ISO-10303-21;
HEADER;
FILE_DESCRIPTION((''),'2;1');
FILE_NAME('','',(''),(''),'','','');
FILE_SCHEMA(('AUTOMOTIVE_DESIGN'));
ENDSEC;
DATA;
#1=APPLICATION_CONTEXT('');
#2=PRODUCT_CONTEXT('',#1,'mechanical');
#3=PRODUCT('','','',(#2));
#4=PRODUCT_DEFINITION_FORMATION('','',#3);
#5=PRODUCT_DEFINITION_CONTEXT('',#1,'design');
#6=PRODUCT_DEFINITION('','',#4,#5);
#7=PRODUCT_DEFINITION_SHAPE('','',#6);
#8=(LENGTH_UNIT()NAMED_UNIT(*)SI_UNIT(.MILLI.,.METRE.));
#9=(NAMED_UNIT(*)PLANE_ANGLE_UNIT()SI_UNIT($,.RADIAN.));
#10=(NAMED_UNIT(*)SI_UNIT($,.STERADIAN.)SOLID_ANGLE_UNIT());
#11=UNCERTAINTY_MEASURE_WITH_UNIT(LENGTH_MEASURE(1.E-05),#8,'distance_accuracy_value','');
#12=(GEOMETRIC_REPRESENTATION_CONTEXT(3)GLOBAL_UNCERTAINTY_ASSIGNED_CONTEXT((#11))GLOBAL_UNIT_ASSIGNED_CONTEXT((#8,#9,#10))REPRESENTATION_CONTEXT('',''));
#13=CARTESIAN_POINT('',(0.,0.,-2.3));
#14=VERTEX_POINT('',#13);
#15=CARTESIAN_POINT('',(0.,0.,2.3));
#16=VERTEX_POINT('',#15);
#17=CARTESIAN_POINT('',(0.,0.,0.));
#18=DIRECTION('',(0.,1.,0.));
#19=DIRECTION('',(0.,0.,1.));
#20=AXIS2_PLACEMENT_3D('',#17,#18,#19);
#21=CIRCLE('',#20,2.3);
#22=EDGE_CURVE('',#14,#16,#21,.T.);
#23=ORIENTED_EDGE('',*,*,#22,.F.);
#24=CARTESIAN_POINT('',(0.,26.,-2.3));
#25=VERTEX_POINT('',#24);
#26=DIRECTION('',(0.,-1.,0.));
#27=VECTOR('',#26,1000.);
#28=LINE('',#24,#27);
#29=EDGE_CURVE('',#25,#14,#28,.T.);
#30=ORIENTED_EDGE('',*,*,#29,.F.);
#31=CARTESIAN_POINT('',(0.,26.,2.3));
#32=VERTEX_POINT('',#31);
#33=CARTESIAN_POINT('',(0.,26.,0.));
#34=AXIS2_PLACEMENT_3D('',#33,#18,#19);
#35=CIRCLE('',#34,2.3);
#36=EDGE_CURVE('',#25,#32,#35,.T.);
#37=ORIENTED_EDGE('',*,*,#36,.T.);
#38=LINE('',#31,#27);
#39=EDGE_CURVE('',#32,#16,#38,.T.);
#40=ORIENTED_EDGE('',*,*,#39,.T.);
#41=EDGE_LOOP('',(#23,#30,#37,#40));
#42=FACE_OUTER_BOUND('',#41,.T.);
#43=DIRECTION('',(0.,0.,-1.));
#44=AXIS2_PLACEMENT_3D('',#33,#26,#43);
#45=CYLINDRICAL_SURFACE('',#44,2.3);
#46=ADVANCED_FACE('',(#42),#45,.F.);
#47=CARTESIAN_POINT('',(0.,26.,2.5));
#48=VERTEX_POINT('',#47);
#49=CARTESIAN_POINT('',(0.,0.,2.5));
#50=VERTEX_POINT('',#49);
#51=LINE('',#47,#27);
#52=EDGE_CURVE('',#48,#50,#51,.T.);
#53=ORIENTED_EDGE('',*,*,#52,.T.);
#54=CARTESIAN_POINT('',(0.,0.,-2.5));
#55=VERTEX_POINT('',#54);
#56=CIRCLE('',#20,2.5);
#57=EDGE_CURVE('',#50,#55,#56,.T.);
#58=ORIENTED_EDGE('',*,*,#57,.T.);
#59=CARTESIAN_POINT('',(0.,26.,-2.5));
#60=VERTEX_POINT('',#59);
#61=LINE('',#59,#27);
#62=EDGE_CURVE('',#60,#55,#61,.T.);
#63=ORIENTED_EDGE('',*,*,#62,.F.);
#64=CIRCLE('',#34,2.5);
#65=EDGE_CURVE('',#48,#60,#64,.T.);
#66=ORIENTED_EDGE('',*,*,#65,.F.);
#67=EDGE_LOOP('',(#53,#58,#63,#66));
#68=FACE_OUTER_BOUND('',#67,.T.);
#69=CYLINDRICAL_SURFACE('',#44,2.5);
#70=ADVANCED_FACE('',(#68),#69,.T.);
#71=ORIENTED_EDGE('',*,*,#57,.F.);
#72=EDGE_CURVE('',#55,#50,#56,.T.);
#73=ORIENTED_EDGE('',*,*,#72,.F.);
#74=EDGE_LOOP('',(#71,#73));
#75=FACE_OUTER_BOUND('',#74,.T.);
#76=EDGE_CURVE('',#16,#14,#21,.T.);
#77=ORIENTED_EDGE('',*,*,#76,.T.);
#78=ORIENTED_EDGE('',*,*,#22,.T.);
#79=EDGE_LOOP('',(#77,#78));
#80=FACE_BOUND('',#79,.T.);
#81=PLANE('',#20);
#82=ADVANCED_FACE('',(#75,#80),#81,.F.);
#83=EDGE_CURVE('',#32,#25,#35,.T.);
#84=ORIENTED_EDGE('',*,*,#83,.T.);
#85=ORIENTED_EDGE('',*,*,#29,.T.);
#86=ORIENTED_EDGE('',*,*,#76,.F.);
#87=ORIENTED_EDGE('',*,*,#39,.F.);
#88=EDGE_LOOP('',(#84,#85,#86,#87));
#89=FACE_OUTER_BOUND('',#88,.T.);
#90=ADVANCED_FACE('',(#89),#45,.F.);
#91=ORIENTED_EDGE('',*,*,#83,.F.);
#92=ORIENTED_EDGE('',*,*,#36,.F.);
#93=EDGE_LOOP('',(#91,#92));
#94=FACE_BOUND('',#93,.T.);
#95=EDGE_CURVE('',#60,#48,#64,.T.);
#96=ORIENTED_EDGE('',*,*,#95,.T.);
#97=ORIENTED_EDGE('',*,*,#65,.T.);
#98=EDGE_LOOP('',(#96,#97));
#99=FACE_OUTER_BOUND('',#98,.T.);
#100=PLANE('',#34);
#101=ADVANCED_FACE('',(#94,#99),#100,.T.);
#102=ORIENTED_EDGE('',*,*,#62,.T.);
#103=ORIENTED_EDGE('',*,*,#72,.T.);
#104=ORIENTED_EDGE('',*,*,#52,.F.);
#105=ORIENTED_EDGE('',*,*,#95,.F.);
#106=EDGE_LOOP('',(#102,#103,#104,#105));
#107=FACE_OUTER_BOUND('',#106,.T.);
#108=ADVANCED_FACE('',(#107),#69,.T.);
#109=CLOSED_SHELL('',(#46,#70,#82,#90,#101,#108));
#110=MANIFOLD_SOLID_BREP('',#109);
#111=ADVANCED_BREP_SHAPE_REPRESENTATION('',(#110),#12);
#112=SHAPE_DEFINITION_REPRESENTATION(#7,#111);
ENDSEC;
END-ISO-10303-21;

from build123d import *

# Parameters (mm, degrees)
SKETCH_1_R      = 2.5
SKETCH_1_R_2    = 2.3
EXTRUDE_1_DEPTH = 26


with BuildPart() as part:
    # 草图1 → 凸台-拉伸1 (new body)
    with BuildSketch(Plane(origin=(0, 0, 0), x_dir=(1, 0, 0), z_dir=(0, 1, 0))):
        with Locations(Location((0, 0, 0), (0, 0, 90))):
            Circle(SKETCH_1_R)
        with Locations(Location((0, 0, 0), (0, 0, 90))):
            Circle(SKETCH_1_R_2, mode=Mode.SUBTRACT)
    extrude(amount=EXTRUDE_1_DEPTH)


solid = part.part
